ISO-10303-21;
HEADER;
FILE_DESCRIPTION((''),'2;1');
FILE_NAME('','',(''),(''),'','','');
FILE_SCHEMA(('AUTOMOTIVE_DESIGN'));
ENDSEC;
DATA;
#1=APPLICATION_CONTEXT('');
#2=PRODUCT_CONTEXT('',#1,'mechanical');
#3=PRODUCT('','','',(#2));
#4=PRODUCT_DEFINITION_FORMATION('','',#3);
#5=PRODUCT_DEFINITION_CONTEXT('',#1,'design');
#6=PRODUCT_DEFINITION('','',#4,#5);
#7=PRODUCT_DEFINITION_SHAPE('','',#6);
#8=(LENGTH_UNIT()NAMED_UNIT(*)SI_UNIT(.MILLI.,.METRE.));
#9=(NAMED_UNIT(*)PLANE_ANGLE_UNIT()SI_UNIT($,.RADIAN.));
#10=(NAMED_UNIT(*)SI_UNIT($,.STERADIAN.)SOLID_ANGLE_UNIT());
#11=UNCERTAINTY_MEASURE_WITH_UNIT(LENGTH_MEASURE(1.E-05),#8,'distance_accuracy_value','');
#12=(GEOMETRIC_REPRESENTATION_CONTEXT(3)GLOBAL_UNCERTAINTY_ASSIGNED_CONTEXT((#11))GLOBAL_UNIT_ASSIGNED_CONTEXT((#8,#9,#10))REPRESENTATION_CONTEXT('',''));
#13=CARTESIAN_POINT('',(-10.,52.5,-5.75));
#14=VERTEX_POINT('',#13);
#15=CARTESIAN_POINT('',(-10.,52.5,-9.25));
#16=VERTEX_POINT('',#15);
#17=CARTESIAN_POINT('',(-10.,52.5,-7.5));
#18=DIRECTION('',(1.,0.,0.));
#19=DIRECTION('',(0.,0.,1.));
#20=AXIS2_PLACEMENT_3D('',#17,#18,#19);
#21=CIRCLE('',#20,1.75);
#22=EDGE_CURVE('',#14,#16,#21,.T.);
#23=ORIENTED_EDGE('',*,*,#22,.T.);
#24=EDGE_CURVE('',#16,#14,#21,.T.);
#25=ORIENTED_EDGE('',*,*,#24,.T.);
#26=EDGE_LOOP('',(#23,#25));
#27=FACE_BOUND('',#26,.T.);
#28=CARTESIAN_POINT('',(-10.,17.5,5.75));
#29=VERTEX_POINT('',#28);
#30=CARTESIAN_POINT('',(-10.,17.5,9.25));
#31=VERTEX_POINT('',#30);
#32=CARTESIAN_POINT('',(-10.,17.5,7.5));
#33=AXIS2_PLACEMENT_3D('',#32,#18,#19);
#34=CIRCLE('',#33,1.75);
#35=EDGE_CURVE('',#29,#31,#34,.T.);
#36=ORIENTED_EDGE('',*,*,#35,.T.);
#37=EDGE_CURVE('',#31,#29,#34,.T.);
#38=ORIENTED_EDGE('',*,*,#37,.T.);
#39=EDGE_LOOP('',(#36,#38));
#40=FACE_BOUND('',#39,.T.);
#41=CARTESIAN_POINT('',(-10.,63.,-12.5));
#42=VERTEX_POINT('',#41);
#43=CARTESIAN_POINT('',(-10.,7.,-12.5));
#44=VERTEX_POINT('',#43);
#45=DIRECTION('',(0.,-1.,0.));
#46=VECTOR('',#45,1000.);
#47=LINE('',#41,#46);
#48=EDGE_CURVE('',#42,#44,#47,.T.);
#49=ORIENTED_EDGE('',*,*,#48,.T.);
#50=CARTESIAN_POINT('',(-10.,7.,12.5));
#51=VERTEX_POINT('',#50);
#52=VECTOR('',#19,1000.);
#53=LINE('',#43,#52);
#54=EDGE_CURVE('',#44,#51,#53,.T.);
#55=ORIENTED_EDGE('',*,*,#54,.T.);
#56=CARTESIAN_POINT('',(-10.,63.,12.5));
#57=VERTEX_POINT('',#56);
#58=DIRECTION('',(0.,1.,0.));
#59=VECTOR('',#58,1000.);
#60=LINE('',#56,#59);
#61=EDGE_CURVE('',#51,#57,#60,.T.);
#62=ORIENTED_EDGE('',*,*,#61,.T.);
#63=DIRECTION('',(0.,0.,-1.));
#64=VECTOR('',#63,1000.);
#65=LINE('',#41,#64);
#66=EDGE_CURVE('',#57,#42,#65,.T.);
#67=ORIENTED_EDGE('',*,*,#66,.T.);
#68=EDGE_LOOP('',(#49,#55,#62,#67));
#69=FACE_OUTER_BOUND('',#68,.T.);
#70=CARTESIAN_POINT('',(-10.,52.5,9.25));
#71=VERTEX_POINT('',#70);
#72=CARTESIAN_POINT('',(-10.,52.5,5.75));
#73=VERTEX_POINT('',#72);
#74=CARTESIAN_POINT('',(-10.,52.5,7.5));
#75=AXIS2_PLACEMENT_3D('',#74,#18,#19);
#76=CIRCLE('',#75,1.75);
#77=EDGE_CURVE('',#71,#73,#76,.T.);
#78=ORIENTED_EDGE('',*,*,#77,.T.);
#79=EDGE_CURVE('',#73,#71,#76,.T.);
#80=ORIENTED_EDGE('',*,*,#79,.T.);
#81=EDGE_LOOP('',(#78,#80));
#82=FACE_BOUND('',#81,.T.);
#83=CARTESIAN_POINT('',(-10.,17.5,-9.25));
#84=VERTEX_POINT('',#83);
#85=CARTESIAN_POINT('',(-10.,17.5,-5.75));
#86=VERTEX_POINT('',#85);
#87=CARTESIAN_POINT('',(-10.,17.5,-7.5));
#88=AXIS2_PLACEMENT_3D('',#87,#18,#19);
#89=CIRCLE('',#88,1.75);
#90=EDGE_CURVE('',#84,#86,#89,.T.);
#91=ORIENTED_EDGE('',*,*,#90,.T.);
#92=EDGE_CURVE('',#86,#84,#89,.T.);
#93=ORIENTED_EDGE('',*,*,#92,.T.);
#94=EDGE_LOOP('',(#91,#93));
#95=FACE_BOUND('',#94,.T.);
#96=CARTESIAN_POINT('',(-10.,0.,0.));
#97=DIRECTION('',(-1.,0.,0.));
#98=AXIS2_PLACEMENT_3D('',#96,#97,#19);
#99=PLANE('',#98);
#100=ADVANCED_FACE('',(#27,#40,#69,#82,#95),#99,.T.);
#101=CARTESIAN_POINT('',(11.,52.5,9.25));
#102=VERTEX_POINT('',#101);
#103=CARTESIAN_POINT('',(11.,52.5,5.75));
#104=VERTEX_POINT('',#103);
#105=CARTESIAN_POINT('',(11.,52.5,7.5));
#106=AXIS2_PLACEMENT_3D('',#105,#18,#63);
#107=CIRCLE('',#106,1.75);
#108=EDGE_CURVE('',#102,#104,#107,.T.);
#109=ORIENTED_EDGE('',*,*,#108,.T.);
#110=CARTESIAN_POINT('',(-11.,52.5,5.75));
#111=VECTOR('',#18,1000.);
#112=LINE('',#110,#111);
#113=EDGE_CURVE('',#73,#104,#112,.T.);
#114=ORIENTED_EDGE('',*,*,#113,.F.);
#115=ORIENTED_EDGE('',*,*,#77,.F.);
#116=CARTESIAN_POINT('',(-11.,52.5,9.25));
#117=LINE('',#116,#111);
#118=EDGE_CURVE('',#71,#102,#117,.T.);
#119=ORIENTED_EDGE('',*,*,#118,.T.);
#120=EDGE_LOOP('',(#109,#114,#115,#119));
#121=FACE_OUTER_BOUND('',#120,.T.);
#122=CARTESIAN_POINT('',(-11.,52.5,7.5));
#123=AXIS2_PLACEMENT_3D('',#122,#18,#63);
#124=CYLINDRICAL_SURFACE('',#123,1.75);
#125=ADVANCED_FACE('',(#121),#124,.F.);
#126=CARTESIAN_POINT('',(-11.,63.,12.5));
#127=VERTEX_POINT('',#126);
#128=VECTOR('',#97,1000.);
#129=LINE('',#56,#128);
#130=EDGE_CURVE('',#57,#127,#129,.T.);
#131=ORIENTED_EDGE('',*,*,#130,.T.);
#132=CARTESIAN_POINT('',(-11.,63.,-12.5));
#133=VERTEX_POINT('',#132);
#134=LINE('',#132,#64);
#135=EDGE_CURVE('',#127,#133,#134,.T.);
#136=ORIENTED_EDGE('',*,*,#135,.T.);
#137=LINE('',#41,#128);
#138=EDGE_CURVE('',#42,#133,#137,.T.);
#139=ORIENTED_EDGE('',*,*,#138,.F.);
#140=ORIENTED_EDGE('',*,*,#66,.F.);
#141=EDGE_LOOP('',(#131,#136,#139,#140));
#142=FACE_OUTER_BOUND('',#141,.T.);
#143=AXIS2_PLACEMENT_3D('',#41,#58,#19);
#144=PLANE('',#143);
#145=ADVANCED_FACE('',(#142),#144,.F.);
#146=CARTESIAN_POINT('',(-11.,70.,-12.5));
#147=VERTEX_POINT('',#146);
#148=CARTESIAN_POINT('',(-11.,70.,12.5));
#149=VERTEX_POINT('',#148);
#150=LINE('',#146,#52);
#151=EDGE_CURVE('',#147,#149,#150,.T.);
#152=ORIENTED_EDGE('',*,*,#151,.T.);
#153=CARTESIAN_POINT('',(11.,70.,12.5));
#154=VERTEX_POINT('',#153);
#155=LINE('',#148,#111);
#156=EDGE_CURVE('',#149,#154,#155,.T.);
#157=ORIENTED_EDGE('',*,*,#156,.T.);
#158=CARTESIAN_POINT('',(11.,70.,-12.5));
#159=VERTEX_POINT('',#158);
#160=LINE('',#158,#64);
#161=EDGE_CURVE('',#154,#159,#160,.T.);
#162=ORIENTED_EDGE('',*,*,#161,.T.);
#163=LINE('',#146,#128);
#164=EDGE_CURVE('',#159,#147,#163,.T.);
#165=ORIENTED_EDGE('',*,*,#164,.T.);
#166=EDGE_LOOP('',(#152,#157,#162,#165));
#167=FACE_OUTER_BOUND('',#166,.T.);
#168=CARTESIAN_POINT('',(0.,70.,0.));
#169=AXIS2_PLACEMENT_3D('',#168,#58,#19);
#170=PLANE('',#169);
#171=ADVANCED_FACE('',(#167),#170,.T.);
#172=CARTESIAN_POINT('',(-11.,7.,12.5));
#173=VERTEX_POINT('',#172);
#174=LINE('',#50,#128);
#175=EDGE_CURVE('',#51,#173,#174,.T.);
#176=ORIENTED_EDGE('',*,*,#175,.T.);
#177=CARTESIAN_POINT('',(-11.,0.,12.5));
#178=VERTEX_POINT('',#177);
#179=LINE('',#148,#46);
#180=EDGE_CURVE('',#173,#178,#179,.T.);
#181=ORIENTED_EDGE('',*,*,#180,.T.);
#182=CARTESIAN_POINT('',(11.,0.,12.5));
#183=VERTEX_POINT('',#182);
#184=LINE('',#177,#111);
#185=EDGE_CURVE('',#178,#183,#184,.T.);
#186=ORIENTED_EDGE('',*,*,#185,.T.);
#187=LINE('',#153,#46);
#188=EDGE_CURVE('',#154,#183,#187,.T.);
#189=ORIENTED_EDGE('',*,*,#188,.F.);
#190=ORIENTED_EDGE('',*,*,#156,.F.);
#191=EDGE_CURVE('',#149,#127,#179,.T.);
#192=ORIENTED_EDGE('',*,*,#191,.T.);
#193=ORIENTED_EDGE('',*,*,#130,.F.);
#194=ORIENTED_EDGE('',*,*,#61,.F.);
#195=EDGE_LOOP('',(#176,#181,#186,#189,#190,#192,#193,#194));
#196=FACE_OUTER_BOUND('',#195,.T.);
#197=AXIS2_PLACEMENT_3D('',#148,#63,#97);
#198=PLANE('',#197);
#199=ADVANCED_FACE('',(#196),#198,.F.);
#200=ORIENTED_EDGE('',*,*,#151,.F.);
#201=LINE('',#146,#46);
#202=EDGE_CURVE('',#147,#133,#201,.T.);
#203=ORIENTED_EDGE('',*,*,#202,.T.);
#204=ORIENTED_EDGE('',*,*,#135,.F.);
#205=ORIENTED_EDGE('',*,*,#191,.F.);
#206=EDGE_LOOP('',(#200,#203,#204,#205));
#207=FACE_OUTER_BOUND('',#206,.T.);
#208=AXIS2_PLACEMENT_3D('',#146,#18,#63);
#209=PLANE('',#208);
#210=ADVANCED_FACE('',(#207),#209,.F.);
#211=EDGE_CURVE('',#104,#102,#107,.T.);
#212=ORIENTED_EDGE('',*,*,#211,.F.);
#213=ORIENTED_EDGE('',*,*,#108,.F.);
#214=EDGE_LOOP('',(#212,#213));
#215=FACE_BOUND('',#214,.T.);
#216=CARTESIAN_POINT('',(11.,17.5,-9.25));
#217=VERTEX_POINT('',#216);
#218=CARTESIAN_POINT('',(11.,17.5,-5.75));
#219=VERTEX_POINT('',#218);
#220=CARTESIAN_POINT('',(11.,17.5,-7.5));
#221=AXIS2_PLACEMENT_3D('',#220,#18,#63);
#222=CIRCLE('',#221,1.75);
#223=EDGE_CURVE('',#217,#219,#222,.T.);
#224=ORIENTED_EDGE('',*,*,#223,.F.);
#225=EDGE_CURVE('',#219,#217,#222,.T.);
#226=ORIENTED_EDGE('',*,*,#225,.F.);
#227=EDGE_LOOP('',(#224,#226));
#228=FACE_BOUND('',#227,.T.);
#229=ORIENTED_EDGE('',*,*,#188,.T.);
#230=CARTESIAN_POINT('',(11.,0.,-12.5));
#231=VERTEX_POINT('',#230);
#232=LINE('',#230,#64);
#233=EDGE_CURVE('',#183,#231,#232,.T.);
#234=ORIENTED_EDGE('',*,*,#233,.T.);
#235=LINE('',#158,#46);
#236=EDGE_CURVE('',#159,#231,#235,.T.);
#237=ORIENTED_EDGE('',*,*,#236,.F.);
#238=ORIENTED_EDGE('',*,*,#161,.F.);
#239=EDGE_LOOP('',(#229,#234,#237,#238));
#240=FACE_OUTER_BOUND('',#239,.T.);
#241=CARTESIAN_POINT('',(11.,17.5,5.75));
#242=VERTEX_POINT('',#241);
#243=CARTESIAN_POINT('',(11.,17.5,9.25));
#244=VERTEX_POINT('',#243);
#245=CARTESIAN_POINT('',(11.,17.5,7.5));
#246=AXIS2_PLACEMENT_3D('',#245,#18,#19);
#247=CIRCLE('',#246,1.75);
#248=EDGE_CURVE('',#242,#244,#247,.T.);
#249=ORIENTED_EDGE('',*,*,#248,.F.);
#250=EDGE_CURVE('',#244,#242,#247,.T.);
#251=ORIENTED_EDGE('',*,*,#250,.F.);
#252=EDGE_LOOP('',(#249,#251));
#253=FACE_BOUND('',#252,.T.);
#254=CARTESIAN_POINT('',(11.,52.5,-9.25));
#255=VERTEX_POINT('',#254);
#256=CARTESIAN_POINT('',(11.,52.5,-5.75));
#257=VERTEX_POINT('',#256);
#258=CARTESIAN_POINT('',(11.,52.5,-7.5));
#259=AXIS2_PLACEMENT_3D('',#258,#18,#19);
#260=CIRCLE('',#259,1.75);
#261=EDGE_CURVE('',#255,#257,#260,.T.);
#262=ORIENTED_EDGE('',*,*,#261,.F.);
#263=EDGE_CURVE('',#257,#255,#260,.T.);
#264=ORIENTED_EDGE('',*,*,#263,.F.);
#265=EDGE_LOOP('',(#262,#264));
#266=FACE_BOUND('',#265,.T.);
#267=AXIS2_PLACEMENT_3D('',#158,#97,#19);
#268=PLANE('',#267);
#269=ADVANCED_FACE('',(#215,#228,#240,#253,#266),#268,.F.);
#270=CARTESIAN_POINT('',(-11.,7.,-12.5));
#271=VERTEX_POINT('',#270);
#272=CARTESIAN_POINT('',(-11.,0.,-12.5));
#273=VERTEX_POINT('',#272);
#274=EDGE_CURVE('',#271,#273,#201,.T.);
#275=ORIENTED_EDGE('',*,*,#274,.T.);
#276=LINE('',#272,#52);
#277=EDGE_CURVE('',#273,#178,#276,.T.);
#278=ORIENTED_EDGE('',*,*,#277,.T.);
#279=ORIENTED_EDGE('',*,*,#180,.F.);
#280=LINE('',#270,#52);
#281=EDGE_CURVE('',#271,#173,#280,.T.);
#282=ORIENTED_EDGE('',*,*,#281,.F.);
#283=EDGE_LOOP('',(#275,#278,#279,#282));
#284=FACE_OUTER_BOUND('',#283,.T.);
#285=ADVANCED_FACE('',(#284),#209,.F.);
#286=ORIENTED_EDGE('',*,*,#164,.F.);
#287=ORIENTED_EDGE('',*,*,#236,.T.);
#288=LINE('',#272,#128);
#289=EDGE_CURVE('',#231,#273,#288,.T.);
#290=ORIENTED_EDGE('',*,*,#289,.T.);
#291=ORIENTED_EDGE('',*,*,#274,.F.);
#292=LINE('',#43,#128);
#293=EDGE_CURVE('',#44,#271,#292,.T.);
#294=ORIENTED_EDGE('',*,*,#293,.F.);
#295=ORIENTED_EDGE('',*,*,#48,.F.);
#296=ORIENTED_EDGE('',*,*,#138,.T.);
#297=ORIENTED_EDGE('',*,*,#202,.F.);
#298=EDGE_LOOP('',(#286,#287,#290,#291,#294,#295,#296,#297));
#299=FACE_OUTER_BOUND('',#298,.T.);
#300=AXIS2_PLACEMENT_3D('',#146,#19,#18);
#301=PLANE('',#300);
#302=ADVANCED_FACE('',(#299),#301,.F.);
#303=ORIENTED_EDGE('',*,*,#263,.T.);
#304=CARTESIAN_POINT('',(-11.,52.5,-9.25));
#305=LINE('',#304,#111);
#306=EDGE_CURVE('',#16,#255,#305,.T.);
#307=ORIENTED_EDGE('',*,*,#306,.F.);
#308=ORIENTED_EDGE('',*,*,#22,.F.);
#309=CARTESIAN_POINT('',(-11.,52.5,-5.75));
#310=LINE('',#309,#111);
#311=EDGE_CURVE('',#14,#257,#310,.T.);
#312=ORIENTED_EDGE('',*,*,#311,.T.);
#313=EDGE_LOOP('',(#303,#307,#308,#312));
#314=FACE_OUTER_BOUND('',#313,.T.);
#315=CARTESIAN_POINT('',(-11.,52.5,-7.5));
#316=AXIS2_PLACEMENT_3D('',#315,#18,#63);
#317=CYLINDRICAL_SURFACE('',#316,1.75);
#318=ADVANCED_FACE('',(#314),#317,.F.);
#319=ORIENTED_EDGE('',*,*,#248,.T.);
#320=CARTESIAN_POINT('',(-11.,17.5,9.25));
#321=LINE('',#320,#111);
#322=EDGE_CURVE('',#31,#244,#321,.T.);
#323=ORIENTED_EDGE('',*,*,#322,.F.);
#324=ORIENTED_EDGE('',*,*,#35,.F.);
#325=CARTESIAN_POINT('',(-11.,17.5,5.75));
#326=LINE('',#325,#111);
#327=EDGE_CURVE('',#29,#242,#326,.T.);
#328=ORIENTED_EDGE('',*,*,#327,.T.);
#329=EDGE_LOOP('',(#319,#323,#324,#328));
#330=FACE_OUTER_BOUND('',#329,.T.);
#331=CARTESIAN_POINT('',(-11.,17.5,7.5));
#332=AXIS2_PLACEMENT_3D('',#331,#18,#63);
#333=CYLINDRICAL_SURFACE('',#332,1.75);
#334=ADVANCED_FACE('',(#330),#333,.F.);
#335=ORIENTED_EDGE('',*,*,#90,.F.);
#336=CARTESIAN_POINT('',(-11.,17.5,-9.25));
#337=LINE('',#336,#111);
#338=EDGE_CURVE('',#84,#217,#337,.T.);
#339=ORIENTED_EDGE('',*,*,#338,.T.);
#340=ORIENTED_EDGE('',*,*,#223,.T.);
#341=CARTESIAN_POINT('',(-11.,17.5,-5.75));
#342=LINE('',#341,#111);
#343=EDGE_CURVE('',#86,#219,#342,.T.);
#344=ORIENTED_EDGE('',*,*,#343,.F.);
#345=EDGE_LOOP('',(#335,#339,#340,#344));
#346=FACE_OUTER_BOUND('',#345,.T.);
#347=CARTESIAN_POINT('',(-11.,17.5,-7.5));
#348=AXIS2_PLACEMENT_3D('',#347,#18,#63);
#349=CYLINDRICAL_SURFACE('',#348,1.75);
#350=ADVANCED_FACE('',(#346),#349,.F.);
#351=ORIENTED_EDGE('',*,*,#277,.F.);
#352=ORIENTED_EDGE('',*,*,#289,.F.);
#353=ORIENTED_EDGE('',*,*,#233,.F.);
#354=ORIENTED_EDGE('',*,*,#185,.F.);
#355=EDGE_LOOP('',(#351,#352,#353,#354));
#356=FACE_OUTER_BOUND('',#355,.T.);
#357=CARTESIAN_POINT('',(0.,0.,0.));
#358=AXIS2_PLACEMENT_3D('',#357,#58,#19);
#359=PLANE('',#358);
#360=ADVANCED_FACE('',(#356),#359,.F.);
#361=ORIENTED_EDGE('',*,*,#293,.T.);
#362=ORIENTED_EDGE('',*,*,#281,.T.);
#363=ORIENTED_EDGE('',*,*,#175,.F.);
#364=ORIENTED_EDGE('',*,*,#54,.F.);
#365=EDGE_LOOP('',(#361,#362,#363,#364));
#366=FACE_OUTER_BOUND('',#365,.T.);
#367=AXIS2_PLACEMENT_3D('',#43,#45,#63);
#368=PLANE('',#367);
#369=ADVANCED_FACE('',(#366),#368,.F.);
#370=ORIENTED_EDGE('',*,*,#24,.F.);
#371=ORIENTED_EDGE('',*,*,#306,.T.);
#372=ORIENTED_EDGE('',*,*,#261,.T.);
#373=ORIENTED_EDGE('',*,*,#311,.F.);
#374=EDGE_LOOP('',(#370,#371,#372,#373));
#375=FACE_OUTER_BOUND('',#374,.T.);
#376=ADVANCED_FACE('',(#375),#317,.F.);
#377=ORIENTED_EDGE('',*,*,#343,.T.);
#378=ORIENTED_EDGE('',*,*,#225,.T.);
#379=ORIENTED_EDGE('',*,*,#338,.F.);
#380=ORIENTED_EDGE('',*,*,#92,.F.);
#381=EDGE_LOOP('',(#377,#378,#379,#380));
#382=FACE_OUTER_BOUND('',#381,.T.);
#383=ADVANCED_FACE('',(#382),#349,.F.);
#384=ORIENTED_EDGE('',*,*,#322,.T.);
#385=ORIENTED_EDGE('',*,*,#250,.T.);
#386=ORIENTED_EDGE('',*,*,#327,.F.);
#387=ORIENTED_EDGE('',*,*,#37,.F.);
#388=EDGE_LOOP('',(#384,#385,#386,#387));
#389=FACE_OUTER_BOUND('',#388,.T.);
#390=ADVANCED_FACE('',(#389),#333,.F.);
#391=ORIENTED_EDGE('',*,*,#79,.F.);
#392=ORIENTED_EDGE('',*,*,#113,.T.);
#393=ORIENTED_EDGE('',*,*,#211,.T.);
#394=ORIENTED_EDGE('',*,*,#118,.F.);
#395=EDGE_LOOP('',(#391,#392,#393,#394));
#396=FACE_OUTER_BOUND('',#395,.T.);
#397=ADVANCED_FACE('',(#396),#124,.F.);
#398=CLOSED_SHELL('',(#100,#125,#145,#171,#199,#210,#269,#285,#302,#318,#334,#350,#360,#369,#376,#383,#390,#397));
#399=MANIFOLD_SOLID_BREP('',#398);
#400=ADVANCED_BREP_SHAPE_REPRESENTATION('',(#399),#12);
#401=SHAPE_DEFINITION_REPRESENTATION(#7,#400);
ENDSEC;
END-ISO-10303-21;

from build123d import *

# Parameters (mm, degrees)
SKETCH1_W           = 22
SKETCH1_H           = 25
BOSS_EXTRUDE1_DEPTH = 70
SKETCH2_R           = 1.75
CUT_EXTRUDE1_DEPTH  = 75.432855649
SKETCH4_W           = 25
SKETCH4_H           = 56
CUT_EXTRUDE3_DEPTH  = 1


with BuildPart() as part:
    # Sketch1 → Boss-Extrude1 (new body)
    with BuildSketch(Plane(origin=(0, 0, 0), x_dir=(1, 0, 0), z_dir=(0, 1, 0))):
        Rectangle(SKETCH1_W, SKETCH1_H)
    extrude(amount=BOSS_EXTRUDE1_DEPTH)

    # Sketch2 → Cut-Extrude1 (cut, through all)
    with BuildSketch(Plane(origin=(11, 0, 0), x_dir=(0, 0, -1), z_dir=(1, 0, 0))):
        with Locations((-7.5, 52.5)):
            Circle(SKETCH2_R)
        with Locations(Location((7.5, 52.5, 0), (0, 0, 180))):
            Circle(SKETCH2_R)
        with Locations((7.5, 17.5)):
            Circle(SKETCH2_R)
        with Locations(Location((-7.5, 17.5, 0), (0, 0, 180))):
            Circle(SKETCH2_R)
    extrude(amount=-CUT_EXTRUDE1_DEPTH, mode=Mode.SUBTRACT)

    # Sketch4 → Cut-Extrude3 (cut)
    with BuildSketch(Plane.ZY.offset(11)):
        with Locations((0, 35)):
            Rectangle(SKETCH4_W, SKETCH4_H)
    extrude(amount=-CUT_EXTRUDE3_DEPTH, mode=Mode.SUBTRACT)


solid = part.part
